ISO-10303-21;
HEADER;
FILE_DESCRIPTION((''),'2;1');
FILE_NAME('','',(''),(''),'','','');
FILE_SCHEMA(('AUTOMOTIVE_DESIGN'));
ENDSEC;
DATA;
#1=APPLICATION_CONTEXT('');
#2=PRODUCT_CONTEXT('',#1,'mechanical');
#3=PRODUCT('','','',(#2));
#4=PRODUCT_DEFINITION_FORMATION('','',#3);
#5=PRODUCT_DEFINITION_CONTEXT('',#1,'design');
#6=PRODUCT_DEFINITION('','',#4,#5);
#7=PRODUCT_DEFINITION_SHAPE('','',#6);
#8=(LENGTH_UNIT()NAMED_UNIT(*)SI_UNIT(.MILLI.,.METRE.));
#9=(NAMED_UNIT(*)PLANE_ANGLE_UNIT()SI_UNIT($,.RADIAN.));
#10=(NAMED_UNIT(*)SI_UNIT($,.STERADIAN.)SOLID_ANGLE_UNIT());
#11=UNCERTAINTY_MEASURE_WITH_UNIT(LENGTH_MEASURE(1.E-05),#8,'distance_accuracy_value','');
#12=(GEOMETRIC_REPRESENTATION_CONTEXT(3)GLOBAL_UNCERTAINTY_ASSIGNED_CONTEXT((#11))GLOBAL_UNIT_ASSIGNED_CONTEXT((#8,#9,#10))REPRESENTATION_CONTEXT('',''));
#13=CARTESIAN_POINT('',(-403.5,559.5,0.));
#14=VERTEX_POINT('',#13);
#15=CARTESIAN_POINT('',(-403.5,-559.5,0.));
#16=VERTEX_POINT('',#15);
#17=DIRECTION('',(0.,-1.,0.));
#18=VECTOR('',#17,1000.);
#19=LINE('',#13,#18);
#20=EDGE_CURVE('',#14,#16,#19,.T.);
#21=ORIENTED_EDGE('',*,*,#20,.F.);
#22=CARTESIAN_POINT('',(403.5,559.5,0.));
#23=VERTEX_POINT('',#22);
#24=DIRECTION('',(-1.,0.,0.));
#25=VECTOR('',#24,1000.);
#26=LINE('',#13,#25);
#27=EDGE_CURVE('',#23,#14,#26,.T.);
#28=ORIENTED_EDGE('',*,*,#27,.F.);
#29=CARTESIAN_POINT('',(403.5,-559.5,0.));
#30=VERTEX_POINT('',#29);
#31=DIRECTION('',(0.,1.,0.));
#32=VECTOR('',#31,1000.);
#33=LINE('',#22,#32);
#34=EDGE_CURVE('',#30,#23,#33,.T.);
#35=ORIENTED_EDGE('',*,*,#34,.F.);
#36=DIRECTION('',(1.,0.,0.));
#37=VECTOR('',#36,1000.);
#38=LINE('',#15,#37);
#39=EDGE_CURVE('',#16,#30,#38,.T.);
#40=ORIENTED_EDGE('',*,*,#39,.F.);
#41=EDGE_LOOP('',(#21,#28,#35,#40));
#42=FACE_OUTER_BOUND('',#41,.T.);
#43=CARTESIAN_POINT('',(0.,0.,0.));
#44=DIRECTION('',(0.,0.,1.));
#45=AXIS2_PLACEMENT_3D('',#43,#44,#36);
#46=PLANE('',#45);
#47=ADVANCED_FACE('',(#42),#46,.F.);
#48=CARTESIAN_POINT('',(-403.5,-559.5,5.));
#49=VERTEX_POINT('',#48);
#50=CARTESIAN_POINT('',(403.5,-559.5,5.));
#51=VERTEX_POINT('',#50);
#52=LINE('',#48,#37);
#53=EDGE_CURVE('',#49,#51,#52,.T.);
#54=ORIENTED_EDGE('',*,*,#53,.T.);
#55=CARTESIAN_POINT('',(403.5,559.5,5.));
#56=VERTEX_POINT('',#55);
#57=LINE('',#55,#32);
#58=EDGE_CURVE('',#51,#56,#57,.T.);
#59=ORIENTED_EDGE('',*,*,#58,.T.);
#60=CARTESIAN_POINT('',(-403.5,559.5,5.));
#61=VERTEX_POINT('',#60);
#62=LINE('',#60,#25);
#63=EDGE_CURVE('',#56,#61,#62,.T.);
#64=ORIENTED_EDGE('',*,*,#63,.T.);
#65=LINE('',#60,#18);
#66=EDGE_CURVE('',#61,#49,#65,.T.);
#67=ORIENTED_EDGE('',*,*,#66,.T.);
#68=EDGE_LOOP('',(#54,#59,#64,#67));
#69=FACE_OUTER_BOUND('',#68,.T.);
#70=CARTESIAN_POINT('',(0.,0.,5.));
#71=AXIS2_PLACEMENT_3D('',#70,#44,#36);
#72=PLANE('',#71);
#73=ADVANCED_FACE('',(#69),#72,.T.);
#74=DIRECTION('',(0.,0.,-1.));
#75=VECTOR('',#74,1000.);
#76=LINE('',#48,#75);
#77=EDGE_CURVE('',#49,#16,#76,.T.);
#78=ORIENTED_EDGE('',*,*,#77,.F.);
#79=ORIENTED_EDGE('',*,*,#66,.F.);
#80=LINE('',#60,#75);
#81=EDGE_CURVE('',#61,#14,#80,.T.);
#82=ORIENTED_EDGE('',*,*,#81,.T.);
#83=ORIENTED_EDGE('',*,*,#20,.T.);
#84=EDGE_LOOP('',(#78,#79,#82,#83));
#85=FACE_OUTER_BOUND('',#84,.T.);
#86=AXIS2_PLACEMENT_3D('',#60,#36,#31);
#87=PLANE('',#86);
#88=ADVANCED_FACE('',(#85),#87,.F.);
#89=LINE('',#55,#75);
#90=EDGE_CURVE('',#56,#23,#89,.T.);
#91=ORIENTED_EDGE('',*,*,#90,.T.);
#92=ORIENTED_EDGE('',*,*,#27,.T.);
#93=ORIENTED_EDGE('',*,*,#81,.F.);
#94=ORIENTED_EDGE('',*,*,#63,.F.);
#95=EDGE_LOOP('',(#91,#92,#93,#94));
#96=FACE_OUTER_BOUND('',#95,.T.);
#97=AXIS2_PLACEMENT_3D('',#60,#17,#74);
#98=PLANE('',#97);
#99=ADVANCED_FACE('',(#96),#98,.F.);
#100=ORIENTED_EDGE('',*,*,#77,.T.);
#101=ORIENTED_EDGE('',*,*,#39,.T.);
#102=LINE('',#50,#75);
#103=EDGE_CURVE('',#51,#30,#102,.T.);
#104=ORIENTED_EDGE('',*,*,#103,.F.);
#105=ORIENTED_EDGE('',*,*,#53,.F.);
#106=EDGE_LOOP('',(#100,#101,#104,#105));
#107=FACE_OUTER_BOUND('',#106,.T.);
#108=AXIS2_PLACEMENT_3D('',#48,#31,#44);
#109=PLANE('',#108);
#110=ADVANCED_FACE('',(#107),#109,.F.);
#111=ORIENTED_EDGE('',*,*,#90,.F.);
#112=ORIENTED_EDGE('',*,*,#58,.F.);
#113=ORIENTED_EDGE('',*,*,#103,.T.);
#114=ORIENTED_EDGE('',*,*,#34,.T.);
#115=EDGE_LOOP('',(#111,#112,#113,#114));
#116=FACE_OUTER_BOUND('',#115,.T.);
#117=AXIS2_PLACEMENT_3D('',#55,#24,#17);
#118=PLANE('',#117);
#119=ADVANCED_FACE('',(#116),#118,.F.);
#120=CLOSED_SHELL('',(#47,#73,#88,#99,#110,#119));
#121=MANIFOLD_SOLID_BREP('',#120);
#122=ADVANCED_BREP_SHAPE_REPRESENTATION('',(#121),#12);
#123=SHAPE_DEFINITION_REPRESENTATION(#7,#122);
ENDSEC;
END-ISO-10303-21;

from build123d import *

# Parameters (mm, degrees)
SKETCH_1_W      = 807
SKETCH_1_H      = 1119
EXTRUDE_1_DEPTH = 5


with BuildPart() as part:
    # 草图1 → 凸台-拉伸1 (new body)
    with BuildSketch(Plane.XY):
        Rectangle(SKETCH_1_W, SKETCH_1_H)
    extrude(amount=EXTRUDE_1_DEPTH)


solid = part.part
